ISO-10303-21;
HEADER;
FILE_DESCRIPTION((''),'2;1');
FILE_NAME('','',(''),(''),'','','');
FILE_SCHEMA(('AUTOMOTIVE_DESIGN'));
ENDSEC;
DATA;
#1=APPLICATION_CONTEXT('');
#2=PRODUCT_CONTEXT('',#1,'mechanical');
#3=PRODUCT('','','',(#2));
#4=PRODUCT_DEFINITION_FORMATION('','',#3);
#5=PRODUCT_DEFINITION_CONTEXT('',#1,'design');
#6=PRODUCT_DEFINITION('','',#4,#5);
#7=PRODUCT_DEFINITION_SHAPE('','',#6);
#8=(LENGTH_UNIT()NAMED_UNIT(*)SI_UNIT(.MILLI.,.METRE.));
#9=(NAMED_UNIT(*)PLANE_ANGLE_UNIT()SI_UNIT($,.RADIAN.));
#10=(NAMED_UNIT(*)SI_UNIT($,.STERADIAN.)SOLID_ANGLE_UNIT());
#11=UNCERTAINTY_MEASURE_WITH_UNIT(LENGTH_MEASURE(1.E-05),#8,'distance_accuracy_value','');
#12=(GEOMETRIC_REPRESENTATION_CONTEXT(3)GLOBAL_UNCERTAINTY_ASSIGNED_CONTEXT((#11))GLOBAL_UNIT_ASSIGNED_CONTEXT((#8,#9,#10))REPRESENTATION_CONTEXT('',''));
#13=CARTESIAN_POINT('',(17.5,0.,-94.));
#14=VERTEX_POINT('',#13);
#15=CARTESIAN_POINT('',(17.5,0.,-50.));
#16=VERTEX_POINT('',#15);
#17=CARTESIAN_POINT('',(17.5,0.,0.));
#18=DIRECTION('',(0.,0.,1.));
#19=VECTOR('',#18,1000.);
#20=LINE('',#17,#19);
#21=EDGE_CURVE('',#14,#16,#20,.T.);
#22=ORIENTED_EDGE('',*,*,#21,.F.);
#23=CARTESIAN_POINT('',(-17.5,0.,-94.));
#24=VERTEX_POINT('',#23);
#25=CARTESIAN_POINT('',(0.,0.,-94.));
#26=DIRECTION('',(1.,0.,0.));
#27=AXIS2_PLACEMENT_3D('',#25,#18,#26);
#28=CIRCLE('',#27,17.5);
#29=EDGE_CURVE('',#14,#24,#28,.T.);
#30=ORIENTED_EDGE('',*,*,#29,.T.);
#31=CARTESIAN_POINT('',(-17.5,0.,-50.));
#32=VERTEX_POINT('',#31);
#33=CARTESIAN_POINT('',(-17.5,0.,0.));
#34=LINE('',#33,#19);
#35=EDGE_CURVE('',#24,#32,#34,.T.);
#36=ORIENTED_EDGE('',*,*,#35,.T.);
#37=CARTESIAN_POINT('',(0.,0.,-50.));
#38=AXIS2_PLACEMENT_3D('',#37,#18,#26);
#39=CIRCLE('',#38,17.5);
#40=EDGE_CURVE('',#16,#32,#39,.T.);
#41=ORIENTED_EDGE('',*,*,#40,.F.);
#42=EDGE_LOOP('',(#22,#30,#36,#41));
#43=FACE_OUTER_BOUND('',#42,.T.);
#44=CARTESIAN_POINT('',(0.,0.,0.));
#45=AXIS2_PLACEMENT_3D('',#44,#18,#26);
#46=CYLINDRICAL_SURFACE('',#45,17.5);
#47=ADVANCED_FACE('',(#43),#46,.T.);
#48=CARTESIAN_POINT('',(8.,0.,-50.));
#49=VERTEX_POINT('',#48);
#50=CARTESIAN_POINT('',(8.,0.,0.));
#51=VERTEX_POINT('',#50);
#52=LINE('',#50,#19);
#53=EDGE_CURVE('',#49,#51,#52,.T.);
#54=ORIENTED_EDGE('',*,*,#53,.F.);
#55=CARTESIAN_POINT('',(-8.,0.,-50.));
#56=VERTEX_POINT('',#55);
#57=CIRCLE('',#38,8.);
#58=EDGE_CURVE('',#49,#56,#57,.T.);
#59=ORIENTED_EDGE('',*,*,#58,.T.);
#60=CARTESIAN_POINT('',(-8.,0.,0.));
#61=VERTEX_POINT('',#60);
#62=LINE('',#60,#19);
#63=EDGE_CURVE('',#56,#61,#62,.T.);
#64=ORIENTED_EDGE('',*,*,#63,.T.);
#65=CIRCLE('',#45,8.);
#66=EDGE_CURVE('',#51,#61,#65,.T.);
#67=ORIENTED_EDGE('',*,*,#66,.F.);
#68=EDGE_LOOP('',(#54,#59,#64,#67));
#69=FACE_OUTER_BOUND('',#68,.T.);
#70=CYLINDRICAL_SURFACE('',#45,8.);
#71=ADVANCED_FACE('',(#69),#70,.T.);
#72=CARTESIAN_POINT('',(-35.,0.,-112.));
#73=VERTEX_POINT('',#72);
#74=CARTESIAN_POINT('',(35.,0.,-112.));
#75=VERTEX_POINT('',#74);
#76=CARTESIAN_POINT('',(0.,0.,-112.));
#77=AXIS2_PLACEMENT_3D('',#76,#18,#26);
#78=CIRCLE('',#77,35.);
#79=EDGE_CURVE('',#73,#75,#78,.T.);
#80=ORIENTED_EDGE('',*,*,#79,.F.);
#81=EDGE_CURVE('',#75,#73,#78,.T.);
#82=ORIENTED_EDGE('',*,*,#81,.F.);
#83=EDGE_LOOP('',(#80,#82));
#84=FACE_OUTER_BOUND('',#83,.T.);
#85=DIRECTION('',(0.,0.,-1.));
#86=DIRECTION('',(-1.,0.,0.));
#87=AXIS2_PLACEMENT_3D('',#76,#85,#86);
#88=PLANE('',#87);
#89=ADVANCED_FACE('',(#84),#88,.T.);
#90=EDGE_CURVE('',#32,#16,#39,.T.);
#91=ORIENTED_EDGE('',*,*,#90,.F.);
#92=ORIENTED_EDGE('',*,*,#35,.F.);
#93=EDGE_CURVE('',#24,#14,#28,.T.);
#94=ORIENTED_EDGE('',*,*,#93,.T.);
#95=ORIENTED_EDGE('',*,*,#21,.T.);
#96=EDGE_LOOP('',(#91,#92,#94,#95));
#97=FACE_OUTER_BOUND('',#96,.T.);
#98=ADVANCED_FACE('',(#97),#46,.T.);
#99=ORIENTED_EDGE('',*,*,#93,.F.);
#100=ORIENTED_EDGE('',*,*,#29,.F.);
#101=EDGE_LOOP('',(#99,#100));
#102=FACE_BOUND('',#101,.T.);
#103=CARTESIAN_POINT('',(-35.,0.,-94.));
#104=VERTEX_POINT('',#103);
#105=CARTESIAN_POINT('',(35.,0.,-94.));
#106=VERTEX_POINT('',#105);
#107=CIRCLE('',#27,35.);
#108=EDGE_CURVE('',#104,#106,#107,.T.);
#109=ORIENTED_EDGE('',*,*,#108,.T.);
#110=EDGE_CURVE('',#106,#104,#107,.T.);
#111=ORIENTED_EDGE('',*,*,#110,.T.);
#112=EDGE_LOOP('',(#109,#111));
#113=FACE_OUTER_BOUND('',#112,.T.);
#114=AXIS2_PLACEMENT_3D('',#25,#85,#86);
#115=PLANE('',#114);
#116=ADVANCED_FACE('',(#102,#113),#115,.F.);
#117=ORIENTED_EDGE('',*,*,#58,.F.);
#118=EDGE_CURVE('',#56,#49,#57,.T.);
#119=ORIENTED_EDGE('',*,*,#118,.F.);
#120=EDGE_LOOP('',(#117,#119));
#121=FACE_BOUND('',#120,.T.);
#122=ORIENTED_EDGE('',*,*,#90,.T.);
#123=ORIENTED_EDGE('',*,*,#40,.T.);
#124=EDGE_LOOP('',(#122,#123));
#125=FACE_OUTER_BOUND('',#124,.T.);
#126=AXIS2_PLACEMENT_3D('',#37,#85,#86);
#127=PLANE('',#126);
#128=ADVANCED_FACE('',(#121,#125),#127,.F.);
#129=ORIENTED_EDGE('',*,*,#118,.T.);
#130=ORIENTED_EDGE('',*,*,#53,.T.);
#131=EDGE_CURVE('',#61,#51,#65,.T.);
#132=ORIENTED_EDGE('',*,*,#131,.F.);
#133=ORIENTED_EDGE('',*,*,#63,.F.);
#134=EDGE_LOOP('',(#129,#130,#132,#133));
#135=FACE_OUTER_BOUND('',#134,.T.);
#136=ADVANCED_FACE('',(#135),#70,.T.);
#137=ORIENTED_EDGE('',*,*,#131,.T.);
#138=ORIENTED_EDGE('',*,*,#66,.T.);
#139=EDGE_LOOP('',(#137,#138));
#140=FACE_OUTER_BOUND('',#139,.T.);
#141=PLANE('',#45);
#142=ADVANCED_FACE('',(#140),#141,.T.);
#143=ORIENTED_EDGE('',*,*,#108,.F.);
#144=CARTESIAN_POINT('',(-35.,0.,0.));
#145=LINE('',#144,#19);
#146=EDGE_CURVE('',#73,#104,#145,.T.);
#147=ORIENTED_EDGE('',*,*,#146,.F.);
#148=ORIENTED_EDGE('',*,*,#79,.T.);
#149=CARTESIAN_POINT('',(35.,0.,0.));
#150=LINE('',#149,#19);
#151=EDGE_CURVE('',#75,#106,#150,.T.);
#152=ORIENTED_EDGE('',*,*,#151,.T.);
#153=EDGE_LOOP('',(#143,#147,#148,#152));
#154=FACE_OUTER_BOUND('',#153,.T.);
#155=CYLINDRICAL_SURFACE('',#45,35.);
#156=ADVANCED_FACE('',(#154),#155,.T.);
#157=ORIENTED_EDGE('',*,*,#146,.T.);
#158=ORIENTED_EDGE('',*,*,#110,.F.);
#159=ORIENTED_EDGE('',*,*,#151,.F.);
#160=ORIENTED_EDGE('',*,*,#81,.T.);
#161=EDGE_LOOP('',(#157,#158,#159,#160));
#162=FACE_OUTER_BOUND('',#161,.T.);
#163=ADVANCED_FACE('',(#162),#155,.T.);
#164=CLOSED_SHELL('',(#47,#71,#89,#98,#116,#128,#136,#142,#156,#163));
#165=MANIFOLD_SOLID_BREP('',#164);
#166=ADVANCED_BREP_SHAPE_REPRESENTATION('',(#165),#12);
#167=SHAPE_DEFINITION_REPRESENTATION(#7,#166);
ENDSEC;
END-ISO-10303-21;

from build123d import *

# Parameters (mm, degrees)
SKETCH1_W = 8
SKETCH1_H = 50


with BuildPart() as part:
    # Sketch1 → Revolve1 (revolve)
    with BuildSketch(Plane(origin=(0, 0, 0), x_dir=(1, 0, 0), z_dir=(0, 1, 0)), mode=Mode.PRIVATE) as revolve1_sk:
        Polygon((-17.5, 94), (0, 94), (0, 112), (-35, 112), (-35, 94), align=None)
        Polygon((-8, 50), (0, 50), (0, 94), (-17.5, 94), (-17.5, 50), align=None)
        with Locations((-4, 25)):
            Rectangle(SKETCH1_W, SKETCH1_H)
    revolve(revolve1_sk.sketch.rotate(Axis((0, 0, 0), (0, 0, -1)), 180), axis=Axis((0, 0, 0), (0, 0, -1)))


solid = part.part
